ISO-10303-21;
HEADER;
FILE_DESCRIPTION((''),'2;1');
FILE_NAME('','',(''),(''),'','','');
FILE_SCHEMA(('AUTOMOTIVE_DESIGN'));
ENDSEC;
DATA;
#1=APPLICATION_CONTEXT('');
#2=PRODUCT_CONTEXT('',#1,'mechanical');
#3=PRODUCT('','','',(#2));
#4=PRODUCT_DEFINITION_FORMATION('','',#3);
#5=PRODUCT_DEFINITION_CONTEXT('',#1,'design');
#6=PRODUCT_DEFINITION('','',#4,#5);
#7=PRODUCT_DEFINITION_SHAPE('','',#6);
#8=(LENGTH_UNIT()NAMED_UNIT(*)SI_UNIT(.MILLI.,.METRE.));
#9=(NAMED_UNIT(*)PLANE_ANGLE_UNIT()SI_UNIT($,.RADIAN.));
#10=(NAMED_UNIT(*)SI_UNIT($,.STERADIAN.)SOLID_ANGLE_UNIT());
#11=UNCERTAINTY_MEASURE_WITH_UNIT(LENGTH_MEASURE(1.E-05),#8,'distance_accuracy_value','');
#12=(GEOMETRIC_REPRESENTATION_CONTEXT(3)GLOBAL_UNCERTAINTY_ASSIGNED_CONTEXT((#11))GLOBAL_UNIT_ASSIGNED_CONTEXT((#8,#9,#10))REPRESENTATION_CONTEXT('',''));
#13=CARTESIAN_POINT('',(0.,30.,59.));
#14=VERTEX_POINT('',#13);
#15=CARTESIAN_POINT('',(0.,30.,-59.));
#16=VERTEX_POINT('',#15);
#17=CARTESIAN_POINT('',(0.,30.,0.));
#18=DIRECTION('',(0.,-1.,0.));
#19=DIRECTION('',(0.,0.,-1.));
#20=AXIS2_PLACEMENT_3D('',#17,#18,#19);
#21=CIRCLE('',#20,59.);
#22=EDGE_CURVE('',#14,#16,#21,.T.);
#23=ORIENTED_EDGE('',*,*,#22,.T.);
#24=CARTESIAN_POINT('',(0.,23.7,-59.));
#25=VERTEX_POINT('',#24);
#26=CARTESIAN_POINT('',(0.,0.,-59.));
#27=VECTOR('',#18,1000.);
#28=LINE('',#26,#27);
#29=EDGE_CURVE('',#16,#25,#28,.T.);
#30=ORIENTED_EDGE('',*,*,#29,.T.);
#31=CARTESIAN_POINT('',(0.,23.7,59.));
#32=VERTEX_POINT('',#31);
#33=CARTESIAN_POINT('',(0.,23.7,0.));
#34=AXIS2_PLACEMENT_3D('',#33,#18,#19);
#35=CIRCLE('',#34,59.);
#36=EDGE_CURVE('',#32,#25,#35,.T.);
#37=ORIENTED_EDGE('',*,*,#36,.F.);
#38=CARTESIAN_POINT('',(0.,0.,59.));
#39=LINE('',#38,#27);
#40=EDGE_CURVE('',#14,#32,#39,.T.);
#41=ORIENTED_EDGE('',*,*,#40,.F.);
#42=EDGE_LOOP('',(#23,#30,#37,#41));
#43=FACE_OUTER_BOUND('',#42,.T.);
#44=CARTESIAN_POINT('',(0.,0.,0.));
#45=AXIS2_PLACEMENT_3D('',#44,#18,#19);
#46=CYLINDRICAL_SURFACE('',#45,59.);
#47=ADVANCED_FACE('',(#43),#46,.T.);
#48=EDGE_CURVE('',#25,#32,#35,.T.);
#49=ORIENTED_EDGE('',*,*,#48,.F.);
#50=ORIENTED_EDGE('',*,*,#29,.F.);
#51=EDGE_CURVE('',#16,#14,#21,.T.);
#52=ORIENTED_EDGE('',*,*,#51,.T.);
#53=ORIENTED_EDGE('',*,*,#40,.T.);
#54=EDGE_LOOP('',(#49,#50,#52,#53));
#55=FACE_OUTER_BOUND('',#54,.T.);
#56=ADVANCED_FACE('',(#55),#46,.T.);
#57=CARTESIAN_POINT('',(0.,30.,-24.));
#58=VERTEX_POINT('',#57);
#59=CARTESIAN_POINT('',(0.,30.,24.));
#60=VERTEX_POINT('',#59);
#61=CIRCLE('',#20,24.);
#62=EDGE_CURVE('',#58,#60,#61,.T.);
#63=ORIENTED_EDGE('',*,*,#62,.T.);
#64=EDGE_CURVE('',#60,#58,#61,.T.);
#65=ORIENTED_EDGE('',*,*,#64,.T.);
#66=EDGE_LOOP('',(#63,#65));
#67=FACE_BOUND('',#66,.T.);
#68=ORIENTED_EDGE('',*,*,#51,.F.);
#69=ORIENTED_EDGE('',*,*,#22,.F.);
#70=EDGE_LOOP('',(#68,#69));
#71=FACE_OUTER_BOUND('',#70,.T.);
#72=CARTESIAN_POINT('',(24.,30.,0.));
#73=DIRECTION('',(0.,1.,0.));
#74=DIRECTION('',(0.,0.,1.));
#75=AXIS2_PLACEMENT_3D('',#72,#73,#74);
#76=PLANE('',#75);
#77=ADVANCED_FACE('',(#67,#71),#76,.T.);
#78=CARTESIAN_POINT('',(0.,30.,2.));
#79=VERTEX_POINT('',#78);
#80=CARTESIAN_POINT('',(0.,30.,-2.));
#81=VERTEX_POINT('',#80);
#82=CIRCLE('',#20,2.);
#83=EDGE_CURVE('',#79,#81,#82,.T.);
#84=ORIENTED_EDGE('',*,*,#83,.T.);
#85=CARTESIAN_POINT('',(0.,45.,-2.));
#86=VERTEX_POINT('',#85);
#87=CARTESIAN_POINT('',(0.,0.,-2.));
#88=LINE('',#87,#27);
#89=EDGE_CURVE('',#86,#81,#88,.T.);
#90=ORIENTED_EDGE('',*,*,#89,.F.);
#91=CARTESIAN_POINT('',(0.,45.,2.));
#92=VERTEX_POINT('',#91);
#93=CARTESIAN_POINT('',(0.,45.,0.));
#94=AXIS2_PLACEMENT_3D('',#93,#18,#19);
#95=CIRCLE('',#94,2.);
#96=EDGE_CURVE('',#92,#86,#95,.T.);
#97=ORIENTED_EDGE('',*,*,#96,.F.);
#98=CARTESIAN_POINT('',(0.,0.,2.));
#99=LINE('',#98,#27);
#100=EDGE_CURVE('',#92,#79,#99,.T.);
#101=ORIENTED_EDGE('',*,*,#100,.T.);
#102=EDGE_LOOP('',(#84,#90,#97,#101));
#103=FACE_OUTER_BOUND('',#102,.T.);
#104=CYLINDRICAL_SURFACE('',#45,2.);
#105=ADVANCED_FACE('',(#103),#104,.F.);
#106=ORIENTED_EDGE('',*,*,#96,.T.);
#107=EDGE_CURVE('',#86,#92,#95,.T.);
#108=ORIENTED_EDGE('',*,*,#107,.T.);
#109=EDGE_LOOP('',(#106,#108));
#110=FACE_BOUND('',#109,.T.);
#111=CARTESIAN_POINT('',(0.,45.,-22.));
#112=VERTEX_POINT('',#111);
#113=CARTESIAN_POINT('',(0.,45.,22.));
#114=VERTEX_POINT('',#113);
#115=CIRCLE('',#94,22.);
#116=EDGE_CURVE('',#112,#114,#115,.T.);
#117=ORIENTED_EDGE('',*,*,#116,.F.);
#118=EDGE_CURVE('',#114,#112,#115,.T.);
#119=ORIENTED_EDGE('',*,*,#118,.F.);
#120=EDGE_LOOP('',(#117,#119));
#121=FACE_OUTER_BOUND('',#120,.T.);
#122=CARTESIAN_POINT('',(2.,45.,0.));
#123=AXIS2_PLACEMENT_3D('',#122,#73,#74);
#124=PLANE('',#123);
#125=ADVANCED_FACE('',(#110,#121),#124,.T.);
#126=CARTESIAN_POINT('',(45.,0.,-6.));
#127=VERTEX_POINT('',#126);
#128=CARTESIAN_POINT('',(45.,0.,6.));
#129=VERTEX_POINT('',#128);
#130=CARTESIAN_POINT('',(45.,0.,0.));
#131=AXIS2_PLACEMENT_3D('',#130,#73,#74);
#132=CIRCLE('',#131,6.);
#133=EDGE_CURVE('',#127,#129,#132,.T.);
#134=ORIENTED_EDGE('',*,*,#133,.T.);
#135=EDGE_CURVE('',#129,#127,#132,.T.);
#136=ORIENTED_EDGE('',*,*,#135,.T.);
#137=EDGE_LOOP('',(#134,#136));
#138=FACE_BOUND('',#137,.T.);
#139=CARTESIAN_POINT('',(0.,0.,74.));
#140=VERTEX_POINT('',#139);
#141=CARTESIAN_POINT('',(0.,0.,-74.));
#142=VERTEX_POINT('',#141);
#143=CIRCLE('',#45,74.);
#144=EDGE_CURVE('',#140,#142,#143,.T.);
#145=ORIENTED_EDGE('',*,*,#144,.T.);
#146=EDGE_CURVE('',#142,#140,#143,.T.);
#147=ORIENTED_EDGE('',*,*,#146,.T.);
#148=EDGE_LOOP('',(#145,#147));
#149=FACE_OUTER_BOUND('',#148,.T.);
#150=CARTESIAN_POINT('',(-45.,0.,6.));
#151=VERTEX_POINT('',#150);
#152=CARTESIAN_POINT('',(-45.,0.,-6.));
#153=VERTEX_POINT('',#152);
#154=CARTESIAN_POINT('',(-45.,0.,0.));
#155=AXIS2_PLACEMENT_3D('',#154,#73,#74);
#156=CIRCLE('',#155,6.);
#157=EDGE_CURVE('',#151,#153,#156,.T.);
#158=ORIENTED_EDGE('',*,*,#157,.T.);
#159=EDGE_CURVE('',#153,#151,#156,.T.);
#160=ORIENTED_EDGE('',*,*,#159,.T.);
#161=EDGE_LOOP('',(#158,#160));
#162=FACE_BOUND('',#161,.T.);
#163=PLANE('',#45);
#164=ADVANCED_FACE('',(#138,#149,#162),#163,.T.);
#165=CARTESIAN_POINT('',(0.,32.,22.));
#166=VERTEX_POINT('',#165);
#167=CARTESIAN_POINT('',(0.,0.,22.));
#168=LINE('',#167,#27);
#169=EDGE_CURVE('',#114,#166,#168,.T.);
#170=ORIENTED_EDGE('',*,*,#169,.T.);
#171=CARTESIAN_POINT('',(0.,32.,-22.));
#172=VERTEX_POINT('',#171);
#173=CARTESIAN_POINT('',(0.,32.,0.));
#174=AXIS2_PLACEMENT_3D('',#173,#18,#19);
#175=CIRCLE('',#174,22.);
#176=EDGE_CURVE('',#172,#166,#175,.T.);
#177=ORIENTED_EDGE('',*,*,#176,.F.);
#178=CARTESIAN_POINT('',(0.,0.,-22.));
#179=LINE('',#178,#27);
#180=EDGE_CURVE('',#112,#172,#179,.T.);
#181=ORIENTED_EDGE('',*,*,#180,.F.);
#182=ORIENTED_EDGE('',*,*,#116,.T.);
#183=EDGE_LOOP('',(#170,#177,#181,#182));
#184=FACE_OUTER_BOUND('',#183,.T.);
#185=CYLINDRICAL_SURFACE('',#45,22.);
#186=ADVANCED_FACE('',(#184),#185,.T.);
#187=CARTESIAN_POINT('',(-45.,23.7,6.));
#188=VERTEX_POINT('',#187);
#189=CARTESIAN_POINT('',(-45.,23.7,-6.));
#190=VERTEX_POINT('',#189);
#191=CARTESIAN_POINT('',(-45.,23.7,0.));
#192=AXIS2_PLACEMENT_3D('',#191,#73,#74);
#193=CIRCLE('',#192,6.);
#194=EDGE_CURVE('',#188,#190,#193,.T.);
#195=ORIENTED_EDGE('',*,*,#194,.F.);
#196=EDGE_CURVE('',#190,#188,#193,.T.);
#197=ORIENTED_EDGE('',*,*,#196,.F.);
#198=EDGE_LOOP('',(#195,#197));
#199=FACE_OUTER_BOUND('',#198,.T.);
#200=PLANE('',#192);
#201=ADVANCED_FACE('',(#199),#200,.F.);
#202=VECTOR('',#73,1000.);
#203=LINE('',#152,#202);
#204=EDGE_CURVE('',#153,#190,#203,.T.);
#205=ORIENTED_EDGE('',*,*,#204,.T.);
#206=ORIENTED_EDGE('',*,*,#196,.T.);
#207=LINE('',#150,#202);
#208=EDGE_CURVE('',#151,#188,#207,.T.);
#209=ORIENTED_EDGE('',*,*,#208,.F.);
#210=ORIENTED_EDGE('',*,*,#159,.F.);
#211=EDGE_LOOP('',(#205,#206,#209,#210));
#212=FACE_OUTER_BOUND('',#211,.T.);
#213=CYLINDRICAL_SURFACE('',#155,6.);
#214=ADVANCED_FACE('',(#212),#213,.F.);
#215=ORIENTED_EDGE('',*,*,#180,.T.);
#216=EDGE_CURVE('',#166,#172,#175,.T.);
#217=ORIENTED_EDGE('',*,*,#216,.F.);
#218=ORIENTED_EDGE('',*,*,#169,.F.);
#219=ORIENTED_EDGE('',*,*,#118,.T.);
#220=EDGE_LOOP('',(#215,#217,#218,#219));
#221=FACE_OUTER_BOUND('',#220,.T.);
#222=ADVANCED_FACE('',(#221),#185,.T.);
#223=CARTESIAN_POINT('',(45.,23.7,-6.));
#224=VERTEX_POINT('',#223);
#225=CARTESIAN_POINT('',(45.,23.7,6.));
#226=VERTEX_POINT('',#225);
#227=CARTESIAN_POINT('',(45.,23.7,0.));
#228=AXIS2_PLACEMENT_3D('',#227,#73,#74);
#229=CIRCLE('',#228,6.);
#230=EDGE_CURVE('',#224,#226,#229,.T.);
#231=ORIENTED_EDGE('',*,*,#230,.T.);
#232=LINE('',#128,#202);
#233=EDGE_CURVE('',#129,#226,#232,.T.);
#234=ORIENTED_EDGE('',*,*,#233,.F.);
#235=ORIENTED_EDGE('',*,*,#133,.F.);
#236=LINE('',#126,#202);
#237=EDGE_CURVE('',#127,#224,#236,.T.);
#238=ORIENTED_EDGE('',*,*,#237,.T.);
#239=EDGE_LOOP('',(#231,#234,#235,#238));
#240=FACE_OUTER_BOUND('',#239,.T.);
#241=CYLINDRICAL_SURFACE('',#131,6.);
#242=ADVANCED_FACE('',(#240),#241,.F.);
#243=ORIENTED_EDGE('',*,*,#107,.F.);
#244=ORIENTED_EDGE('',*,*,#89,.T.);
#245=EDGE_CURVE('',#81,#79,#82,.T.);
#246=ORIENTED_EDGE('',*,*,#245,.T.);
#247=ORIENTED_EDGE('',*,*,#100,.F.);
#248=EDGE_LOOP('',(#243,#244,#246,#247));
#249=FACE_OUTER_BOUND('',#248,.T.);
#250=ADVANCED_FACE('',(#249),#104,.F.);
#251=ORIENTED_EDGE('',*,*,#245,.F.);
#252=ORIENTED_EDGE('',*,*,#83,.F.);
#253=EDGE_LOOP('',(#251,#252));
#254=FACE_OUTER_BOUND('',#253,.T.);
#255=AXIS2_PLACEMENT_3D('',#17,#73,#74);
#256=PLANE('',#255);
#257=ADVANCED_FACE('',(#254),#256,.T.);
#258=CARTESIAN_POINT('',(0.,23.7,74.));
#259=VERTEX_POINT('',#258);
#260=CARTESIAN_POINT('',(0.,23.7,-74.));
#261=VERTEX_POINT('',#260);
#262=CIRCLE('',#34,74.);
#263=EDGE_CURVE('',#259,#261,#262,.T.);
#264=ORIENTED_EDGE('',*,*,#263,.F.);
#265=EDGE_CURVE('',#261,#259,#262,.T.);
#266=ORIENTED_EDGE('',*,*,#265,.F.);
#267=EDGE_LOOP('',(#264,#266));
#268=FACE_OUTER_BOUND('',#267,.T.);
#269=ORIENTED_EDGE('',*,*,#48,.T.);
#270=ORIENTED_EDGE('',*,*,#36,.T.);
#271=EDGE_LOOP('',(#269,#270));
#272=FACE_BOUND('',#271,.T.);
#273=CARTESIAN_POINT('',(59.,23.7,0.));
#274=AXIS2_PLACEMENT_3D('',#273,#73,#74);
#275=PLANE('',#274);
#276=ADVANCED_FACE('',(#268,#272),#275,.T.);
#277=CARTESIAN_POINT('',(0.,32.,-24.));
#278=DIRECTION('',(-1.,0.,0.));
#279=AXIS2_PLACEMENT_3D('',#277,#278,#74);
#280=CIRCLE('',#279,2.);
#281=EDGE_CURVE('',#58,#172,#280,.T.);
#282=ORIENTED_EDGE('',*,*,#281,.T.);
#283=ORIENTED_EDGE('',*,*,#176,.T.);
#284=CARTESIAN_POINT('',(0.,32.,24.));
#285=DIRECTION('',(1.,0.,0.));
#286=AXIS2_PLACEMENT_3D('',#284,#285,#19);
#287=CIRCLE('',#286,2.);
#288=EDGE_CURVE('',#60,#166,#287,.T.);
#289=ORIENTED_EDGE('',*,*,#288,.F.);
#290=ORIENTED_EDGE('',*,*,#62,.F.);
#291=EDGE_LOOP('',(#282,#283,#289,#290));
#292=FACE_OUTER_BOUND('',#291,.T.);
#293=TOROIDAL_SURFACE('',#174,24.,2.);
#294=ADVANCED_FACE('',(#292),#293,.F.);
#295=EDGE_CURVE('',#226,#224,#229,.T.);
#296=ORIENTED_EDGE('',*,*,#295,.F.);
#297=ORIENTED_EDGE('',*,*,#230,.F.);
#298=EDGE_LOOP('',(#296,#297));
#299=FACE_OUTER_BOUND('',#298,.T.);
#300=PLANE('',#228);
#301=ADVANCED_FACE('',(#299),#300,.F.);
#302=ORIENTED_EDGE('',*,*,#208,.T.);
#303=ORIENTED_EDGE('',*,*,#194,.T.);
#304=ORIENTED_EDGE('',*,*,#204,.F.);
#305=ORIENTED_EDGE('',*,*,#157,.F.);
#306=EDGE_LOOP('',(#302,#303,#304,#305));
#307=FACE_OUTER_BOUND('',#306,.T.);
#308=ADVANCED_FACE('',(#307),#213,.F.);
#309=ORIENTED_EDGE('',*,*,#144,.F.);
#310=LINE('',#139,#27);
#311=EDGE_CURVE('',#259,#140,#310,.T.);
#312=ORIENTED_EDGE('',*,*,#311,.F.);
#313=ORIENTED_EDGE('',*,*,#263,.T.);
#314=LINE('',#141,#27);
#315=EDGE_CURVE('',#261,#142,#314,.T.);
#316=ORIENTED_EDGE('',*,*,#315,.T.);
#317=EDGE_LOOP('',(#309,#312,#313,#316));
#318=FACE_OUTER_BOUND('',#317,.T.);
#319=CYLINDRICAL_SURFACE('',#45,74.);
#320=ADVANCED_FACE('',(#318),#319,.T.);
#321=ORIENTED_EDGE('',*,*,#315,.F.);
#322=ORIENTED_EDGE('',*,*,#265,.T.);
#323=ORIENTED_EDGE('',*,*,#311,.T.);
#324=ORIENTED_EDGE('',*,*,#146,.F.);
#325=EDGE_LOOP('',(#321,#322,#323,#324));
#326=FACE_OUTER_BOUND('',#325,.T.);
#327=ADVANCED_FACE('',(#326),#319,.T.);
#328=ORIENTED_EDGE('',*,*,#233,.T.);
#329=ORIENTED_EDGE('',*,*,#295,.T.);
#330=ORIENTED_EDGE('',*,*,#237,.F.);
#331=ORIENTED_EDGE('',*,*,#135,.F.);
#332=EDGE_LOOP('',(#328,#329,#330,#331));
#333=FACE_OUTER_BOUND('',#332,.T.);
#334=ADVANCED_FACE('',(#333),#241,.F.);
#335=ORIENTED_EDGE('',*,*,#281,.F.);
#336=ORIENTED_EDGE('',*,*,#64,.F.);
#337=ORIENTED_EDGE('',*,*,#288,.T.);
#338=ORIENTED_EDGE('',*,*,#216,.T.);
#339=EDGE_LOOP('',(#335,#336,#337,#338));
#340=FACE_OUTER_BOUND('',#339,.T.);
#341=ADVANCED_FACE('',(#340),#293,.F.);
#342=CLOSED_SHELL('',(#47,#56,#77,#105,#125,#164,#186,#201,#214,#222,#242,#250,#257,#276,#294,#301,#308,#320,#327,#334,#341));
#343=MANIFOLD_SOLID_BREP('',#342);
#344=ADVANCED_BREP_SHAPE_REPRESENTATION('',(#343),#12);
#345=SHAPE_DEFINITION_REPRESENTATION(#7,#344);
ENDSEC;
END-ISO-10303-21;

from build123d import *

# Parameters (mm, degrees)
CENTRE_CUT_SKETCH_R = 6
CENTRE_CUT_DEPTH    = 108.301863917


with BuildPart() as part:
    # Disc Profile Sketch → Stepped Disc Revolve (revolve)
    with BuildSketch(Plane.XY, mode=Mode.PRIVATE) as stepped_disc_revolve_sk:
        with BuildLine():
            Line((0, 0), (0, 30))
            Line((0, 30), (2, 30))
            Line((2, 30), (2, 45))
            Line((2, 45), (22, 45))
            Line((22, 45), (22, 32))
            ThreePointArc((22, 32), (22.585786438, 30.585786438), (24, 30))
            Line((24, 30), (59, 30))
            Line((59, 30), (59, 23.7))
            Line((59, 23.7), (74, 23.7))
            Line((74, 23.7), (74, 0))
            Line((74, 0), (0, 0))
        make_face()
    revolve(stepped_disc_revolve_sk.sketch.rotate(Axis((0, 0, 0), (0, 1, 0)), 90), axis=Axis((0, 0, 0), (0, 1, 0)))

    # Centre Cut Sketch → Centre Cut (cut, through all)
    with BuildSketch(Plane(origin=(0, 23.7, 0), x_dir=(1, 0, 0), z_dir=(0, 1, 0))):
        with Locations(Location((-45, 0, 0), (0, 0, 270))):
            Circle(CENTRE_CUT_SKETCH_R)
        with Locations(Location((45, 0, 0), (0, 0, 270))):
            Circle(CENTRE_CUT_SKETCH_R)
    extrude(amount=-CENTRE_CUT_DEPTH, mode=Mode.SUBTRACT)


solid = part.part
